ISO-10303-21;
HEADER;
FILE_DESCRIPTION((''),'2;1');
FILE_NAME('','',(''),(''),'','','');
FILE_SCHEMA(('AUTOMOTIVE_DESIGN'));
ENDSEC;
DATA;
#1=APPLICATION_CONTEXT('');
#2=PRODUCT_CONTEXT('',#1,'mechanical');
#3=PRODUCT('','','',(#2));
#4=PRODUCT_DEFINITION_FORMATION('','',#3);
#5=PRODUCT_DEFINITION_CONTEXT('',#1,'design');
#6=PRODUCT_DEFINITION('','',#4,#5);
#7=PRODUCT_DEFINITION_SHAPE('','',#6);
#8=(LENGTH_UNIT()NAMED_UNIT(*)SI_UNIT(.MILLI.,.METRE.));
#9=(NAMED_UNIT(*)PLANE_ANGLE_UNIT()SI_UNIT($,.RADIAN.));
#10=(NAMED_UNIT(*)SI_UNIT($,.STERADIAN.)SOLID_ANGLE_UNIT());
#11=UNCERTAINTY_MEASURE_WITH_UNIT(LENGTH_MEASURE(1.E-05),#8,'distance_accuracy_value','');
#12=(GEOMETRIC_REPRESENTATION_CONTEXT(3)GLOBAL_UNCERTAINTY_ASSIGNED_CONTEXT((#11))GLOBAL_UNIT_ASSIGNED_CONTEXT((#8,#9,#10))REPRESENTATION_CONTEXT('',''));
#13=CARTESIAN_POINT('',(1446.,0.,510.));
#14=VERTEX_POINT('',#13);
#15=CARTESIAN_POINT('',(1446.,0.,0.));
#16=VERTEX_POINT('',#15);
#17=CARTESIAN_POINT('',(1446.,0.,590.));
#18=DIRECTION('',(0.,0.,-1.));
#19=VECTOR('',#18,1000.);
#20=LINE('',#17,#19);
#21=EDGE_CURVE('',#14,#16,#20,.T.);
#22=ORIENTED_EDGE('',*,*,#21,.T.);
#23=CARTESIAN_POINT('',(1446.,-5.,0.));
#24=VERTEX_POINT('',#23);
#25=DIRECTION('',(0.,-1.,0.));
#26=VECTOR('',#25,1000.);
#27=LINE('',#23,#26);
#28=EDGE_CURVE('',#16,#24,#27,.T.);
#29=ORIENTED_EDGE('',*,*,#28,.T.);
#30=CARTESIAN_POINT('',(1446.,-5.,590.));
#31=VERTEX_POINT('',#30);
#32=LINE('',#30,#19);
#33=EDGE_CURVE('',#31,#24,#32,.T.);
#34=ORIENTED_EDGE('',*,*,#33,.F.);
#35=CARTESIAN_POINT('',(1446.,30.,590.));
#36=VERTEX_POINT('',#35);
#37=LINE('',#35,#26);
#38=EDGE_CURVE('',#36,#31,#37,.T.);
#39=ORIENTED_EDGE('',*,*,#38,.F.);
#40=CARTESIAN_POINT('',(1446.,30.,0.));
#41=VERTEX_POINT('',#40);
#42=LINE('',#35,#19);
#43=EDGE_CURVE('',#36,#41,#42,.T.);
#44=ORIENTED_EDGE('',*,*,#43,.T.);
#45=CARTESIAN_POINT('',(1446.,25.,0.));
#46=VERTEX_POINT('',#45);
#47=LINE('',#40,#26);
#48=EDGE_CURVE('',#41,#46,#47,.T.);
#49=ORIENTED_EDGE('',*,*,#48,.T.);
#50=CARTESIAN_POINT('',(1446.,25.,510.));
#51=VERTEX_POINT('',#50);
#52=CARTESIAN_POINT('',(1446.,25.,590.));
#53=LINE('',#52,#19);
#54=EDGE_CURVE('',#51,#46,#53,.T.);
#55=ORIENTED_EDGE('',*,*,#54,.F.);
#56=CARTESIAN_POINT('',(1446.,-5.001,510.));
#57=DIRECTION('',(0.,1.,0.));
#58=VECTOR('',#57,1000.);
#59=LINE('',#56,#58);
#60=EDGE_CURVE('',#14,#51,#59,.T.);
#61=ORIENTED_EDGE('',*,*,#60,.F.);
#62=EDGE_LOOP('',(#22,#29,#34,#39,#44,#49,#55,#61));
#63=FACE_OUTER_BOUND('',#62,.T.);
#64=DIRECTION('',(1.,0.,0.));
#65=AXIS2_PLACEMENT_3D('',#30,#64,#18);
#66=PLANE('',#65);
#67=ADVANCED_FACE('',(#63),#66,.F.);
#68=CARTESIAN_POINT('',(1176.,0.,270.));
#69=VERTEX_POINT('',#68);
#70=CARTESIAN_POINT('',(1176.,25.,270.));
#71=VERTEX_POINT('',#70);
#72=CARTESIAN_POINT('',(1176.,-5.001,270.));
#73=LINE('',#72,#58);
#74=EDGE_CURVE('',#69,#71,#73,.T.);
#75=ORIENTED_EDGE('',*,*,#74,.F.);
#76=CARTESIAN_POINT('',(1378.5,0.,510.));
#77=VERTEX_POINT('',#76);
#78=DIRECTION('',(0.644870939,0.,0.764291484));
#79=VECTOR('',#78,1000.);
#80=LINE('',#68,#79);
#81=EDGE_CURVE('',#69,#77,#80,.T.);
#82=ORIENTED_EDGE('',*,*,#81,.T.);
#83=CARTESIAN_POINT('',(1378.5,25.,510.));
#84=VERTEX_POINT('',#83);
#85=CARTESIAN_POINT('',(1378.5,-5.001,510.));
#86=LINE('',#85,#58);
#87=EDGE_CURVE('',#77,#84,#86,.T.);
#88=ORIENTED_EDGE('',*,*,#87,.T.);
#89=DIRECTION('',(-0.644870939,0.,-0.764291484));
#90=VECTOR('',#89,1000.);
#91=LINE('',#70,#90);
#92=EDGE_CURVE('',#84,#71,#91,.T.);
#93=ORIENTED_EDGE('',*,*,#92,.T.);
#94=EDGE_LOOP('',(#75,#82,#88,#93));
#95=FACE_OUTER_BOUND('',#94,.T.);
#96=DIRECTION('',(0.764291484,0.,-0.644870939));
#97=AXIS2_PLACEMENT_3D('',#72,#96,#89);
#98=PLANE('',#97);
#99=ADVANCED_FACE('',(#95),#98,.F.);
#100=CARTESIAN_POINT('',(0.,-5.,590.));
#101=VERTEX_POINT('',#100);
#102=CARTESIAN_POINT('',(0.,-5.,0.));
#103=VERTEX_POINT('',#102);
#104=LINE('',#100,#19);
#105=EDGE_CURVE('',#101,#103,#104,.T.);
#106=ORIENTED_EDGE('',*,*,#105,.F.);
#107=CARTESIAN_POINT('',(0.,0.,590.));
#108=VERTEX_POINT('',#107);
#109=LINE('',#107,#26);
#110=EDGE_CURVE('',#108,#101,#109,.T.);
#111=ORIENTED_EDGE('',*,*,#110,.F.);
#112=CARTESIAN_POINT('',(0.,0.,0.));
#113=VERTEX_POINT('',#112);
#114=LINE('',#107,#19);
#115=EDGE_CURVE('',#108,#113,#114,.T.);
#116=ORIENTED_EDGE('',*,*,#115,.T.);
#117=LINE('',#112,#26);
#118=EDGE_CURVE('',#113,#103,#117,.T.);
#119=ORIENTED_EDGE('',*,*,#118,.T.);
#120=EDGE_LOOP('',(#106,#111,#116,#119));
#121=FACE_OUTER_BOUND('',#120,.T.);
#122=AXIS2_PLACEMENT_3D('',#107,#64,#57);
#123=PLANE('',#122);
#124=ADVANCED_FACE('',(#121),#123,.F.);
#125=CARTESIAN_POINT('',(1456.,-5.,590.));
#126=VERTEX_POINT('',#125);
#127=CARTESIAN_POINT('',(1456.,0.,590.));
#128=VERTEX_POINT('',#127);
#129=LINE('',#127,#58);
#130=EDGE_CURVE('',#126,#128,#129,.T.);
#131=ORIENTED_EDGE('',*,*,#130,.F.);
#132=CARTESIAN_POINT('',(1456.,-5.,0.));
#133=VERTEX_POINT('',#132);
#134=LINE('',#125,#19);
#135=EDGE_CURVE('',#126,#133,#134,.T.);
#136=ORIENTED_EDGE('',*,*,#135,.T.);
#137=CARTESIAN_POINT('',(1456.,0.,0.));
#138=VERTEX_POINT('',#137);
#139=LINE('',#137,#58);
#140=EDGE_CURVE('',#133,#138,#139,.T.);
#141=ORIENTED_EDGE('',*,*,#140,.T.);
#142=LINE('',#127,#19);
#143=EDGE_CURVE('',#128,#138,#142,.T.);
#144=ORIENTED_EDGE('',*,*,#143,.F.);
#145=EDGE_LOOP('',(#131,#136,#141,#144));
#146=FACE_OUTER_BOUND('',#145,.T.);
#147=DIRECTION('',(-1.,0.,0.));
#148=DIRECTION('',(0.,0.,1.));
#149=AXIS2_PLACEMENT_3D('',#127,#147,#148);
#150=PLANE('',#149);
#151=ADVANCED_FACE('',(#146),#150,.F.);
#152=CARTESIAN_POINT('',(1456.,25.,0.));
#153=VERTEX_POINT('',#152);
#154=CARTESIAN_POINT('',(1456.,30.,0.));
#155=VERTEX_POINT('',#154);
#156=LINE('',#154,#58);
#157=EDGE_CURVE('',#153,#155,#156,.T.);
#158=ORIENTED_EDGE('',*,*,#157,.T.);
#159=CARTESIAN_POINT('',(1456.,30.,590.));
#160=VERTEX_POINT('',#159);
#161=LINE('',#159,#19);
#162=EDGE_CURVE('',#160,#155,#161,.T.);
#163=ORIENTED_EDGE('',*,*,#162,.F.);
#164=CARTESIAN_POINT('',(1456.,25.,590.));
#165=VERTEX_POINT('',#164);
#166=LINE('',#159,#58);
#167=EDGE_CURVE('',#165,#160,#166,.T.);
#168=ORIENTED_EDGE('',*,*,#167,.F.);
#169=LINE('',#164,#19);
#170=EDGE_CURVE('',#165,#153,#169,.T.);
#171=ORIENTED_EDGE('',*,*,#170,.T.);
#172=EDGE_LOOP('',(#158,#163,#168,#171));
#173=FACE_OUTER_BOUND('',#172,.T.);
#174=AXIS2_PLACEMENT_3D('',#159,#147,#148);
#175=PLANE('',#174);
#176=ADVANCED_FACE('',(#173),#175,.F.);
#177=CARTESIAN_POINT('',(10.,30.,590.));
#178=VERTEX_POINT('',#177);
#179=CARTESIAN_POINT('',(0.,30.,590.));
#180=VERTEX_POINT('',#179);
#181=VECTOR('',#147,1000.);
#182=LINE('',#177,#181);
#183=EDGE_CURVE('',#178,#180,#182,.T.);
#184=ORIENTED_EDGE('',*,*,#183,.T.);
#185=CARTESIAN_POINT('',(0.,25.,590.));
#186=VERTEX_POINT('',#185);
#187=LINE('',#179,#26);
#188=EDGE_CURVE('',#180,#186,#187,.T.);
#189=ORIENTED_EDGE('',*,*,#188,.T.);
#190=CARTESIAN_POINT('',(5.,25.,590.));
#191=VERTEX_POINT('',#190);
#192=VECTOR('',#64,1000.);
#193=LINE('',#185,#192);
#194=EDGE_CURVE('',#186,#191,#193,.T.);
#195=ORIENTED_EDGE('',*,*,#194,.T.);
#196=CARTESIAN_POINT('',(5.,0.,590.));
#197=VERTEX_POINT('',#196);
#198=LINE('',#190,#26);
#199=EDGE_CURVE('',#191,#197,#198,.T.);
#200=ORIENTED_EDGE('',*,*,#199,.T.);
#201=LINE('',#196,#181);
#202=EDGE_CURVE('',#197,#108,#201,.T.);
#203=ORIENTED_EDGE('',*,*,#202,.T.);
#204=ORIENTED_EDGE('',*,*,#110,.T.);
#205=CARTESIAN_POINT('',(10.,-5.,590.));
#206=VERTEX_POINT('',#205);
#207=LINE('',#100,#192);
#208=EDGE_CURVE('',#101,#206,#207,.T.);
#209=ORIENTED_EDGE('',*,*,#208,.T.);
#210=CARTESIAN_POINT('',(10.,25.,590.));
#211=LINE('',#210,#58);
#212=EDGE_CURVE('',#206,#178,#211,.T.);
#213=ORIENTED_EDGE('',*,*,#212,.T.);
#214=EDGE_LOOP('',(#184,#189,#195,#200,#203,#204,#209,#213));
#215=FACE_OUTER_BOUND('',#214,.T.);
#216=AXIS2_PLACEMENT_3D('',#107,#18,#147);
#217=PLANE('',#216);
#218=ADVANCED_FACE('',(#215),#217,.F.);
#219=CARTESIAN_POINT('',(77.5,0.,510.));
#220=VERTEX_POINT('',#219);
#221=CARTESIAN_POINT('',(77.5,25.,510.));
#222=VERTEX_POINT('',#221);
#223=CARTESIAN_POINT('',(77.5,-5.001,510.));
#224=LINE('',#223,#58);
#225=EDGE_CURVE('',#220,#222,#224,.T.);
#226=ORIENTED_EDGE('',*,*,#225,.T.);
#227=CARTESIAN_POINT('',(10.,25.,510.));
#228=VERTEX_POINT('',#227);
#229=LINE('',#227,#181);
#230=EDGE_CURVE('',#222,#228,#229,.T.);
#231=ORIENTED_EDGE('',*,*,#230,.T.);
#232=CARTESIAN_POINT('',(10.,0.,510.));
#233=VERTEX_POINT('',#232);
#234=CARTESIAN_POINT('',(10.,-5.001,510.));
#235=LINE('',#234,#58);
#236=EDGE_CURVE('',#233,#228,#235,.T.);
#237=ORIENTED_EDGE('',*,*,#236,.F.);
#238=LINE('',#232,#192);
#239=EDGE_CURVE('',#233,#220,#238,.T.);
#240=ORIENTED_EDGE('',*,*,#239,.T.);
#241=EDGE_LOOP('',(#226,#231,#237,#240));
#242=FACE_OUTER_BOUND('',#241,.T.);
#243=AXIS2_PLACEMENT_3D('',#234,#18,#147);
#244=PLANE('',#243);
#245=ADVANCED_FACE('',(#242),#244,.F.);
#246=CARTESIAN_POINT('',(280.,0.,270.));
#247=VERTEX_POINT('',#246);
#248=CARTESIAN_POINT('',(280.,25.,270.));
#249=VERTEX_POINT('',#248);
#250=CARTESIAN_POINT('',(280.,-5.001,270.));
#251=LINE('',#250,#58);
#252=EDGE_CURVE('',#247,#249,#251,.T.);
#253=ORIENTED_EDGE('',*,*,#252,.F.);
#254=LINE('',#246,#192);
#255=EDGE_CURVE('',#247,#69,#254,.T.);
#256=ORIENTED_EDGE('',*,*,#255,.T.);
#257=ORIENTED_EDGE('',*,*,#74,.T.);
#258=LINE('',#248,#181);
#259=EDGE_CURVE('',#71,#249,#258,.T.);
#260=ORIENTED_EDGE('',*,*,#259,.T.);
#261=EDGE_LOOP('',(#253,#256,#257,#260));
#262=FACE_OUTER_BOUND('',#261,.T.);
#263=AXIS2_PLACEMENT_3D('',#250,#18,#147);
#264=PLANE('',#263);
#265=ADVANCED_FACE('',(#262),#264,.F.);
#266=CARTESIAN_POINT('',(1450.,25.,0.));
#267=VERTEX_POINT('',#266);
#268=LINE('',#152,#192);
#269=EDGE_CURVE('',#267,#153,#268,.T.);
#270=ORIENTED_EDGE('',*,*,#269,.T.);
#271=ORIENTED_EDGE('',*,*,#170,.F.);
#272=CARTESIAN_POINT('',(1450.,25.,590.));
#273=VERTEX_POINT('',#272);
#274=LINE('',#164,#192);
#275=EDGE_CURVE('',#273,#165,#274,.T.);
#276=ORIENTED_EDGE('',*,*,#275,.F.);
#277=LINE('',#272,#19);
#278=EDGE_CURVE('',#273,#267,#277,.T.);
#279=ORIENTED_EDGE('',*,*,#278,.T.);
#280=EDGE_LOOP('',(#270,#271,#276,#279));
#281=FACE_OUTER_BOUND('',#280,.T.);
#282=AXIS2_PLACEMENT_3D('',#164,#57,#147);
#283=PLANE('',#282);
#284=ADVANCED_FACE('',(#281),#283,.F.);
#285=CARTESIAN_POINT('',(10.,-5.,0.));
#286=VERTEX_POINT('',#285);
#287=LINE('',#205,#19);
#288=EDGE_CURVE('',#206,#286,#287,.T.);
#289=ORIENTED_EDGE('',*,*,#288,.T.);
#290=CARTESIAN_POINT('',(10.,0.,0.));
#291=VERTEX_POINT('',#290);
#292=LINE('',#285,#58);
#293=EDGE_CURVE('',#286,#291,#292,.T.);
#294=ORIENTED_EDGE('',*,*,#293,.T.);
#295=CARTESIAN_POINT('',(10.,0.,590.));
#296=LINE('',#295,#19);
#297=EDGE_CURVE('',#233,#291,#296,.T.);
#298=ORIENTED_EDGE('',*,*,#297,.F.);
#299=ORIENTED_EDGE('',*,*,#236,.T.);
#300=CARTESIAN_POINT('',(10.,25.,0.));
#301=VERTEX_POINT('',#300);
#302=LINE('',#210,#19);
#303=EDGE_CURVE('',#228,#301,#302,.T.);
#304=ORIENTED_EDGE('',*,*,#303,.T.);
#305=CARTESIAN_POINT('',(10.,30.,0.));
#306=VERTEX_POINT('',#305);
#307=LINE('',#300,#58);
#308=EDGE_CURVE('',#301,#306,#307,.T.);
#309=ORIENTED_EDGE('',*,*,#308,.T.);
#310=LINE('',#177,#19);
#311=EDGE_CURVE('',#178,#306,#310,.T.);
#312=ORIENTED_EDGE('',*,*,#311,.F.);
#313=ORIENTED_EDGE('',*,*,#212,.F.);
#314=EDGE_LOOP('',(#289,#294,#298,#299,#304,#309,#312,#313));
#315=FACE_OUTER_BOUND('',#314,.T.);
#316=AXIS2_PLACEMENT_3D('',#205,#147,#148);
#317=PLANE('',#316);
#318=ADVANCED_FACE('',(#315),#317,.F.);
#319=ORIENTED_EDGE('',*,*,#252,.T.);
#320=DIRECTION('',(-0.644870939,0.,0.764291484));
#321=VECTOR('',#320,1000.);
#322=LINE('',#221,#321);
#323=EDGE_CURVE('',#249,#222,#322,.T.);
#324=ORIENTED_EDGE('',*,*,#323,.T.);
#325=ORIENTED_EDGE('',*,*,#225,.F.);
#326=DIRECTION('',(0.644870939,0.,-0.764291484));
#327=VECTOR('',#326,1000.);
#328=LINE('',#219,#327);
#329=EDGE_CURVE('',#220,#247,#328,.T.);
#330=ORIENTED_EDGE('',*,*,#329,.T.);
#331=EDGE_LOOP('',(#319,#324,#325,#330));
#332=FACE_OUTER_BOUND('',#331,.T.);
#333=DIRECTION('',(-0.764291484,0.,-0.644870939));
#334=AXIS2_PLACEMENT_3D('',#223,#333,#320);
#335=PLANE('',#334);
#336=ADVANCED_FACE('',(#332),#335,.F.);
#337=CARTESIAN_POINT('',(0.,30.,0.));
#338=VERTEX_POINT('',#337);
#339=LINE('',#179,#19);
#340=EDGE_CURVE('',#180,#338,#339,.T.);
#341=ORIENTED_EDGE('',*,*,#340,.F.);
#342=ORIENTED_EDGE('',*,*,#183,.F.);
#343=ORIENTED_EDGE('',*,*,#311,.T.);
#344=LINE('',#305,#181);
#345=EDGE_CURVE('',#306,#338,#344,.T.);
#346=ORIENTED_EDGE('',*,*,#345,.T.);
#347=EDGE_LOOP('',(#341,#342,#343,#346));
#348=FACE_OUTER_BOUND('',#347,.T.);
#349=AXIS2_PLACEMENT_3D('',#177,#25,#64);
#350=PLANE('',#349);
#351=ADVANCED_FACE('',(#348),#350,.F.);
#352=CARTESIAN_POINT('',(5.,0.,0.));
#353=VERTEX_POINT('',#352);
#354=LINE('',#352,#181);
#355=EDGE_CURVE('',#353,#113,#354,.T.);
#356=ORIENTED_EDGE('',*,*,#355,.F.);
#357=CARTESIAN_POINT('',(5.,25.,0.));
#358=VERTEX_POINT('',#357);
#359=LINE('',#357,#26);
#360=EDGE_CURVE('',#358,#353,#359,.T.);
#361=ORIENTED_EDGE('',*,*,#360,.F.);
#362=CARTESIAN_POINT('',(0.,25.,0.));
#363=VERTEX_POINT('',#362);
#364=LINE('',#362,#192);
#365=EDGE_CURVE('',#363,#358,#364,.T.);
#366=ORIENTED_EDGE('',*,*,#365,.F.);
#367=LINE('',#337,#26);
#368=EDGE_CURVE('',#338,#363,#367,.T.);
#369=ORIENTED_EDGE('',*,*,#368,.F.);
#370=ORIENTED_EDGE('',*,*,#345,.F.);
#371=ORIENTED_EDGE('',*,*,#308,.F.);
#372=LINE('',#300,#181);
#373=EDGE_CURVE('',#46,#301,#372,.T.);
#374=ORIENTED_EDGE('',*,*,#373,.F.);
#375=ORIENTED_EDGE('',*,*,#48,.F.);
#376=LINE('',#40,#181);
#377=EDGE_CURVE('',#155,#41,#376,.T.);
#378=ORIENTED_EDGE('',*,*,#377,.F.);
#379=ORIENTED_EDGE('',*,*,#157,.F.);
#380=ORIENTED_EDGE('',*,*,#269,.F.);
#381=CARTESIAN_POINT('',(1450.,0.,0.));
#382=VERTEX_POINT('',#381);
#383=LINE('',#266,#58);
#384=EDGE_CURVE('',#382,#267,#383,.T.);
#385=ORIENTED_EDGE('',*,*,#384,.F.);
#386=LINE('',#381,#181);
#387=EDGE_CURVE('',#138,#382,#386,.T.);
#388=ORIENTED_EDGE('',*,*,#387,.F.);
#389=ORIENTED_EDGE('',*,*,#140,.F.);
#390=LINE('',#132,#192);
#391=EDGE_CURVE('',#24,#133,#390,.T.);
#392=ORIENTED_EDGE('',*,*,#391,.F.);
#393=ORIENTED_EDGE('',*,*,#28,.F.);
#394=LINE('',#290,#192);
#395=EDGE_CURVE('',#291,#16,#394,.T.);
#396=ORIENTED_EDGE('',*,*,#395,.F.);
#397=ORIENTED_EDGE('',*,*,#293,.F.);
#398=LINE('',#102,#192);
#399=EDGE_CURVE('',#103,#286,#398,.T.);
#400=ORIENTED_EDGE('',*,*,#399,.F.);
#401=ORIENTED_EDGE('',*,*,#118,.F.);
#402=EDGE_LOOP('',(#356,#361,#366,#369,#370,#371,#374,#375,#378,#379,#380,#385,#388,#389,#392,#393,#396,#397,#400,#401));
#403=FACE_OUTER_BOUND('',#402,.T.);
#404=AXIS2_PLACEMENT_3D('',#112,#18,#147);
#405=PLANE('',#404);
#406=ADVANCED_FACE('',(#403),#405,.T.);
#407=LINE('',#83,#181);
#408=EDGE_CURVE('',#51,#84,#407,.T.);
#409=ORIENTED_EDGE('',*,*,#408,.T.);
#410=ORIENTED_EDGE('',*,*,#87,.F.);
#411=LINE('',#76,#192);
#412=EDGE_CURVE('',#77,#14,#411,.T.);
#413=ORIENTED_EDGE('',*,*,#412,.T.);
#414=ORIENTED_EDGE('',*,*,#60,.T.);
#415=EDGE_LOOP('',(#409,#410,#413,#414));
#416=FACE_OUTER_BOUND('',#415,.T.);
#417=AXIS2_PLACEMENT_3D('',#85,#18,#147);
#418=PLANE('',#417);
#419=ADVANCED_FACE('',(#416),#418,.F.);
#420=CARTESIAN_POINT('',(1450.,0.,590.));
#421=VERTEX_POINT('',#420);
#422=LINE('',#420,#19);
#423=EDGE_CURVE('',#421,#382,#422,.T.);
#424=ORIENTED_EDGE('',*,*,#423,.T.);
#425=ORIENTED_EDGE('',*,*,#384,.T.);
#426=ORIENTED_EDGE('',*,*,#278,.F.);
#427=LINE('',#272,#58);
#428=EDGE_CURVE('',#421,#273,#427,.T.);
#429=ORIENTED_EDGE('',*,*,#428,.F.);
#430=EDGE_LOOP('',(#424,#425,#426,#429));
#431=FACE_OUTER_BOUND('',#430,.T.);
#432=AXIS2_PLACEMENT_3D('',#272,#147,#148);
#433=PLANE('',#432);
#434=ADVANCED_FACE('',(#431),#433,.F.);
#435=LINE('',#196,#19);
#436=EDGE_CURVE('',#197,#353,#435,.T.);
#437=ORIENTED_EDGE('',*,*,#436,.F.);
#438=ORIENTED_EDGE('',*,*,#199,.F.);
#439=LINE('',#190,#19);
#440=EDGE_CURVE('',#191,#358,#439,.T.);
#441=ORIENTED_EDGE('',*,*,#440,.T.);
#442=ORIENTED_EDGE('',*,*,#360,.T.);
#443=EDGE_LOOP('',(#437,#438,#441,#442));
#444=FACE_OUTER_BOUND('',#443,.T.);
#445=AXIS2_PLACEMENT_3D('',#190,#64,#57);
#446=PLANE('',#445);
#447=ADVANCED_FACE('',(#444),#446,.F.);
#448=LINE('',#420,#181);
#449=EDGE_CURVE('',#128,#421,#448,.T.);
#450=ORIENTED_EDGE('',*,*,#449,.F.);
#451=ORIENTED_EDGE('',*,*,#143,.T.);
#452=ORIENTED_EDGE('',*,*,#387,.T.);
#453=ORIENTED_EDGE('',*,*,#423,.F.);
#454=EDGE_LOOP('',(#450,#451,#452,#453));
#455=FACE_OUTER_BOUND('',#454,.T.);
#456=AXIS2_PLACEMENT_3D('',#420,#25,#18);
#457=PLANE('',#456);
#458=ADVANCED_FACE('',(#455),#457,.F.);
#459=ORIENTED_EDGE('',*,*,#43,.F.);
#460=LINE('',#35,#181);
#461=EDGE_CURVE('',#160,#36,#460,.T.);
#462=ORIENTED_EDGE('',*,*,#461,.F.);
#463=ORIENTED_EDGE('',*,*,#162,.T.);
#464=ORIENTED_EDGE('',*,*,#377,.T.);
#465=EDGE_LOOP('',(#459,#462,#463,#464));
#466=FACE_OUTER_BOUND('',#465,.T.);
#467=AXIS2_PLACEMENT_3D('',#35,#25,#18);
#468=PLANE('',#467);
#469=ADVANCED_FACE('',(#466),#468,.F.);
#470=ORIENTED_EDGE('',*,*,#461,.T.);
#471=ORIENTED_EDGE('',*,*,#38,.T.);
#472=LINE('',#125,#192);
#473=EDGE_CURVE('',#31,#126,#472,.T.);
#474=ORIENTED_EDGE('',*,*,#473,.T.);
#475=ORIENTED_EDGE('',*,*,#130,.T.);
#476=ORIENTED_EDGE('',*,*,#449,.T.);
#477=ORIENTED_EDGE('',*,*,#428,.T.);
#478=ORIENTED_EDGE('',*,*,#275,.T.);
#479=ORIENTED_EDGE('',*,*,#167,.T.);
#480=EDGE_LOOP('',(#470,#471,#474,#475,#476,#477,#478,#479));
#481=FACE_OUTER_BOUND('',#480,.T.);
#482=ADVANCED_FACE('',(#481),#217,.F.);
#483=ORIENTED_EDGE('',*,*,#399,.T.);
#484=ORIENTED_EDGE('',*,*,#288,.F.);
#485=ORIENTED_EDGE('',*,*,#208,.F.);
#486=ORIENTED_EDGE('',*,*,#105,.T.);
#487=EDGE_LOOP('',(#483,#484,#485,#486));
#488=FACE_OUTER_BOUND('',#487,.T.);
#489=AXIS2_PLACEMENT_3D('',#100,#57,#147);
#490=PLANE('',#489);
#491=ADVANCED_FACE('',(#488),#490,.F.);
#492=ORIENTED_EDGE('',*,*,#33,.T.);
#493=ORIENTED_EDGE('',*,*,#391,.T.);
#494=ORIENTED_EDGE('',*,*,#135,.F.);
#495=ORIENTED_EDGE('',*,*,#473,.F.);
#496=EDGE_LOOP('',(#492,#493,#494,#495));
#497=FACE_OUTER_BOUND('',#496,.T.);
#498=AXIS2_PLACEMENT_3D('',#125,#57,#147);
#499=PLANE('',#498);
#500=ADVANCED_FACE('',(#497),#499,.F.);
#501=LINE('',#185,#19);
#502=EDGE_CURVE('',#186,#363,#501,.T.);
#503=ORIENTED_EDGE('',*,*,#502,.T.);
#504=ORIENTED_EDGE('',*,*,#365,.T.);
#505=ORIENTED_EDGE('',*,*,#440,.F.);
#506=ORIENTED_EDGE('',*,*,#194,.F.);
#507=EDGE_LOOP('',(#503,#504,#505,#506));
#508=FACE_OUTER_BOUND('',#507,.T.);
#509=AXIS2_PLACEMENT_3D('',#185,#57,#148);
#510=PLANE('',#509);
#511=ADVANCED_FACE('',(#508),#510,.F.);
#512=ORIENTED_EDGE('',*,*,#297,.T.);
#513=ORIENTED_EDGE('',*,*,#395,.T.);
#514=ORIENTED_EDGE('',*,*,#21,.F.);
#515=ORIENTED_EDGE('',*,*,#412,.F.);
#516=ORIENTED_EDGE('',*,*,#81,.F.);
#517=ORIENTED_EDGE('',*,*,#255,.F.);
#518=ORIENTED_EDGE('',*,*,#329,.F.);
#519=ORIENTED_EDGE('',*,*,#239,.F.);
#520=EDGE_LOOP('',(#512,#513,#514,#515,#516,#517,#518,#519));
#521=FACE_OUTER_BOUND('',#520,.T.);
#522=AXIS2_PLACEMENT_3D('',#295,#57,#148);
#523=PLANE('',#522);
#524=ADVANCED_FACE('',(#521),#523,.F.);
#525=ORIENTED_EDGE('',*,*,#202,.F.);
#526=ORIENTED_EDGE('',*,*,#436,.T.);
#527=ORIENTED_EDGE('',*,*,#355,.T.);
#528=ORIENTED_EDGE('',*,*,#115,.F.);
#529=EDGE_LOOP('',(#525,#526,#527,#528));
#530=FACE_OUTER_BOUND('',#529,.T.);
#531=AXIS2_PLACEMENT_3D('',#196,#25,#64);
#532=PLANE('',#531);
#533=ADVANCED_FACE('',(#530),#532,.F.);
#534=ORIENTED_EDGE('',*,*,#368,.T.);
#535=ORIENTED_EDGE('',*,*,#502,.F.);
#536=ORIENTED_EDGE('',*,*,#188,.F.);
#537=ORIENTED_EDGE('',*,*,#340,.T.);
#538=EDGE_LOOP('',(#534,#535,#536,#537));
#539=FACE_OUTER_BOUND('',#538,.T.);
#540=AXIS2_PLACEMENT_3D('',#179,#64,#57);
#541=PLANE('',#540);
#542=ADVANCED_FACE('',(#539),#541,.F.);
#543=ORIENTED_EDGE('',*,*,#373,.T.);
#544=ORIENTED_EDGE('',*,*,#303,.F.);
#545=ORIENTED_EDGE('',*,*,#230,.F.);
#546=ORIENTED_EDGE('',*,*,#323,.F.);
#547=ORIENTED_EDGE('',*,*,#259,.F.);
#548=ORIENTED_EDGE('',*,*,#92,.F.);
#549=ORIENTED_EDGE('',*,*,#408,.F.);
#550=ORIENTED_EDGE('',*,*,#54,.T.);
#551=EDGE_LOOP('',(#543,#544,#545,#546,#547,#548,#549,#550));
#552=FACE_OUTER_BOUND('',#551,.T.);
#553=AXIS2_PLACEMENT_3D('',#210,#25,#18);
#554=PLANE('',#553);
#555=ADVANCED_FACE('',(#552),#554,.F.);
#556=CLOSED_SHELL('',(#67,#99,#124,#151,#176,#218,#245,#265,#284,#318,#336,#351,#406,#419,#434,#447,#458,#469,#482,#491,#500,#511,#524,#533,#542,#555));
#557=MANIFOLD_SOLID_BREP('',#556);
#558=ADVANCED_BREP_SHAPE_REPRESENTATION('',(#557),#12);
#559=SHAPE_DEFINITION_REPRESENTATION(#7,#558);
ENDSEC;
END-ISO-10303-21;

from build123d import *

# Parameters (mm, degrees)
BOSS_EXTRUDE1_DEPTH = 590
CUT_EXTRUDE1_REACH  = 1573.285


with BuildPart() as part:
    # Sketch1 → Boss-Extrude1 (new body)
    with BuildSketch(Plane.XY):
        Polygon((10, 25), (10, 30), (0, 30), (0, 25), (5, 25), (5, 0), (0, 0), (0, -5), (10, -5), (10, 0), (1446, 0), (1446, -5), (1456, -5), (1456, 0), (1450, 0), (1450, 25), (1456, 25), (1456, 30), (1446, 30), (1446, 25), align=None)
    extrude(amount=BOSS_EXTRUDE1_DEPTH)

    # Sketch2 → Cut-Extrude1 (cut, up to next)
    with BuildSketch(Plane(origin=(0, 25, 0), x_dir=(1, 0, 0), z_dir=(0, 1, 0)), mode=Mode.PRIVATE) as cut_extrude1_sk1:
        Polygon((10, -590), (1446, -590), (1446, -510), (1378.5, -510), (1176, -270), (280, -270), (77.5, -510), (10, -510), align=None)
    cut_extrude1_tool1 = extrude(cut_extrude1_sk1.sketch, amount=-CUT_EXTRUDE1_REACH, mode=Mode.PRIVATE) & part.part
    add(cut_extrude1_tool1.solids().sort_by_distance((728, 25, 443.695445))[0], mode=Mode.SUBTRACT)


solid = part.part
